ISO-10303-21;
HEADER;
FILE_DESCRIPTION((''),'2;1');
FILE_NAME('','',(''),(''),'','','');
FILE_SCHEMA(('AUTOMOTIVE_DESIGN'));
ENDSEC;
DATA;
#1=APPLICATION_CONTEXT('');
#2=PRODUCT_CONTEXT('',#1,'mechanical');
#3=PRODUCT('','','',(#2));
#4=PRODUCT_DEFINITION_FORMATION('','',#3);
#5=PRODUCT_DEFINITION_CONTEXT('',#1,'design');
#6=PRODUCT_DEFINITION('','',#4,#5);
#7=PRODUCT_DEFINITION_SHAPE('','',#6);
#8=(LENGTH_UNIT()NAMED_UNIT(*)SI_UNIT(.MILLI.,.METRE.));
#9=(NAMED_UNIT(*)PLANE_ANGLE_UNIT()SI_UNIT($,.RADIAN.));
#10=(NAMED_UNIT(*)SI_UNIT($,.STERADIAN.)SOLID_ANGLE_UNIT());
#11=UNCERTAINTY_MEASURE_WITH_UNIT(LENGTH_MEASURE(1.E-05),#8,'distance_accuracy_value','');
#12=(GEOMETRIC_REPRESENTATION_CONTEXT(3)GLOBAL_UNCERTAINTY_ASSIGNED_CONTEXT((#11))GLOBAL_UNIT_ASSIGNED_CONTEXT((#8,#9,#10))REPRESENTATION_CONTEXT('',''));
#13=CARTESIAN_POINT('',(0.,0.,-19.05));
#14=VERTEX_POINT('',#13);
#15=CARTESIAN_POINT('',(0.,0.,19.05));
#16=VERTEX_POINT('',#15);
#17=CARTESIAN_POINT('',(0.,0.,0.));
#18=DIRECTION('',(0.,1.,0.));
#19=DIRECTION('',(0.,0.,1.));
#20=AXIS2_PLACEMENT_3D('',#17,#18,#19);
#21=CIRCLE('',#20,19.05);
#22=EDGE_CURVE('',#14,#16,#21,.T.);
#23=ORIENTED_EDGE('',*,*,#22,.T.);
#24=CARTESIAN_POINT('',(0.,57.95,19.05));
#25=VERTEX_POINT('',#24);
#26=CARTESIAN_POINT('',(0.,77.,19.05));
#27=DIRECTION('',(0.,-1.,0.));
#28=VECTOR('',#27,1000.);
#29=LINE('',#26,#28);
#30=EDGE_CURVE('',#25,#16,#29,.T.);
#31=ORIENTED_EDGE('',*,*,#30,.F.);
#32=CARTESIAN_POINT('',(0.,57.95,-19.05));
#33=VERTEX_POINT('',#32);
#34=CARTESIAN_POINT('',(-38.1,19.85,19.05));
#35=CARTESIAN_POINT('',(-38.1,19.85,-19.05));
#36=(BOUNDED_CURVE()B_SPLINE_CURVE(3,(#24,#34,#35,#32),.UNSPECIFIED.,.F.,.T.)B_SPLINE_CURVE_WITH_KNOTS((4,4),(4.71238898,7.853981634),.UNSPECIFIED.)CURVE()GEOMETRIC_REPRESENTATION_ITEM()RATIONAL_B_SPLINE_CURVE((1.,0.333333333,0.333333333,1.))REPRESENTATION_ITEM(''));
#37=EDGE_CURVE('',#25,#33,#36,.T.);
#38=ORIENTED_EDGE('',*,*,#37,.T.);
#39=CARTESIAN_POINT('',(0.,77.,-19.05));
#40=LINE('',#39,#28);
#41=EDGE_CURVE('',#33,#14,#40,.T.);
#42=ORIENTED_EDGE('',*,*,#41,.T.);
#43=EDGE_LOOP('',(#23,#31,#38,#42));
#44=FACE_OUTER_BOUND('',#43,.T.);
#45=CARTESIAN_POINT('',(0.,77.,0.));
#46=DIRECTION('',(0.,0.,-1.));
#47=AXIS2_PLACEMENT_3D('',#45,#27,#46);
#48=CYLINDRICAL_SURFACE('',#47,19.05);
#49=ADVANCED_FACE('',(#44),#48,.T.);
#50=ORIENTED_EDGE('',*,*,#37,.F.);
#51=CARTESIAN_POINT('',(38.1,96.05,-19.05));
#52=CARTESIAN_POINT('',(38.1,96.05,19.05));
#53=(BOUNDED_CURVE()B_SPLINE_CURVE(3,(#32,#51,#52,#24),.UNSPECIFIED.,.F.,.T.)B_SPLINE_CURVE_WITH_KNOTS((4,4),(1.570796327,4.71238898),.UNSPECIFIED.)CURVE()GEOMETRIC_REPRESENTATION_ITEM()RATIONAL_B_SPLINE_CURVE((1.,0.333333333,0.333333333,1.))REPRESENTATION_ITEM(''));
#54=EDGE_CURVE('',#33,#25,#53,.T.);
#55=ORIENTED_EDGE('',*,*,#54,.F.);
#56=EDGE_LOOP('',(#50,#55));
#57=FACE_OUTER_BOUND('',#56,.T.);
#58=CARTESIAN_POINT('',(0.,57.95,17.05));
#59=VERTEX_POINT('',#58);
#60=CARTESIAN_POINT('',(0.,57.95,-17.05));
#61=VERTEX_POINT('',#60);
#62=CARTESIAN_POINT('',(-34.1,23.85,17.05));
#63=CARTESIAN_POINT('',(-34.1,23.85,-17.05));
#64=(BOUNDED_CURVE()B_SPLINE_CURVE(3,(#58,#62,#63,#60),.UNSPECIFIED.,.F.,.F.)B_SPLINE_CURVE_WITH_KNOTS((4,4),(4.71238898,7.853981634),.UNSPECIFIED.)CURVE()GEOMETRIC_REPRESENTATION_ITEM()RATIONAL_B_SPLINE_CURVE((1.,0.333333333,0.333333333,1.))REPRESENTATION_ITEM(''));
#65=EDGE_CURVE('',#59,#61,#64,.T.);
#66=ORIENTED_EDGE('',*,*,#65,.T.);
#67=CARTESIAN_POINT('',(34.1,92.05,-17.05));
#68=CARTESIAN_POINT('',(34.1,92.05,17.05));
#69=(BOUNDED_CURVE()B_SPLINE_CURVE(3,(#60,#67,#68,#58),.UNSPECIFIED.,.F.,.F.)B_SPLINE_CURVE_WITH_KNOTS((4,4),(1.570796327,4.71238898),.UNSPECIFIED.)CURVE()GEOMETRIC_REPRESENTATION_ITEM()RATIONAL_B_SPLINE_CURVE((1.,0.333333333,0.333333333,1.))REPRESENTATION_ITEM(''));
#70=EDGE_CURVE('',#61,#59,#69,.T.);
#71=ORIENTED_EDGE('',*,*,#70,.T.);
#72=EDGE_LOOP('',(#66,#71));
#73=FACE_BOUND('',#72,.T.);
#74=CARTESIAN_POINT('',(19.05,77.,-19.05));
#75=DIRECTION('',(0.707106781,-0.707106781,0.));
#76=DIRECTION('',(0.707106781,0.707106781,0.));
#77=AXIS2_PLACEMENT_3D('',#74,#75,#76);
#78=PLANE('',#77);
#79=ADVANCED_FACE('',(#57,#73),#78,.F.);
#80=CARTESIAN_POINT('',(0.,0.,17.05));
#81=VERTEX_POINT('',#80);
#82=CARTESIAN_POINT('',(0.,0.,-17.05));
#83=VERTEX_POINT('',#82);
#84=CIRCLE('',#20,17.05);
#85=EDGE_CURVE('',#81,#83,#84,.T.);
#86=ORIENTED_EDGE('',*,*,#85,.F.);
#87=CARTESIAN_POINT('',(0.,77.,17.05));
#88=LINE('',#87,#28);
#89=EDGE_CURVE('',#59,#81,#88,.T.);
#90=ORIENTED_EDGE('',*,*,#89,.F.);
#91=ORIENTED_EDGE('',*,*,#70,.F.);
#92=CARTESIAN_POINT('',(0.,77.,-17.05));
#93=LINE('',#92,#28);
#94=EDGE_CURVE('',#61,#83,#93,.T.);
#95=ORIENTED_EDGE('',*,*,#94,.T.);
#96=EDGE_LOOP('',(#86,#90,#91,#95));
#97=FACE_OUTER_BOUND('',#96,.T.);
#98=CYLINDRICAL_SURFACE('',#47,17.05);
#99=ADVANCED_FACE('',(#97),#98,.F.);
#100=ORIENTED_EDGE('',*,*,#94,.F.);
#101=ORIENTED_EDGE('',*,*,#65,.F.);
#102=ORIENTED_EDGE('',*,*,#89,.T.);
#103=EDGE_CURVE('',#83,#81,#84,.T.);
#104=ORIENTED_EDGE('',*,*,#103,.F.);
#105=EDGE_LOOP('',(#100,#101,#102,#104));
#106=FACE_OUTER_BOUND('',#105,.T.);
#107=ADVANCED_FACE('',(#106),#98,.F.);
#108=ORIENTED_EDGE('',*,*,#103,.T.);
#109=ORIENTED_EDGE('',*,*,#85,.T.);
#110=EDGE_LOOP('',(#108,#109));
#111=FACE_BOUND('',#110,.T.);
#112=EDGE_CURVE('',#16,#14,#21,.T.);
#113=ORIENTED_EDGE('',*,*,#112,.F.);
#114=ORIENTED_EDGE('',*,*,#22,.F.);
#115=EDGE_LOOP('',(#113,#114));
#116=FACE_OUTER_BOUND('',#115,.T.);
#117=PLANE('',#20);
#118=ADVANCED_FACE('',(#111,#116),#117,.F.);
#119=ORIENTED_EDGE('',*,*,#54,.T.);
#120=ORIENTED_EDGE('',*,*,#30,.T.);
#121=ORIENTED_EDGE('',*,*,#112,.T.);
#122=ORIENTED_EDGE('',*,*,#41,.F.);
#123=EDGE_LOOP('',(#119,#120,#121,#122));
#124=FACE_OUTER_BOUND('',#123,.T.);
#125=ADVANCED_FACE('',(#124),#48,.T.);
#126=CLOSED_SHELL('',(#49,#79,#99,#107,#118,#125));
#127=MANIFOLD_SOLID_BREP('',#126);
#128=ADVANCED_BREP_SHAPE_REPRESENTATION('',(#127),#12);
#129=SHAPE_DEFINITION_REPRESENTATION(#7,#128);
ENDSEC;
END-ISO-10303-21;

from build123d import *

# Parameters (mm, degrees)
SKETCH1_R               = 19.05
SKETCH1_R_2             = 17.05
BOSS_EXTRUDE1_DEPTH     = 77
CUT_EXTRUDE1_DEPTH      = 82.576988177
CUT_EXTRUDE1_DEPTH_BACK = 82.576988177


with BuildPart() as part:
    # Sketch1 → Boss-Extrude1 (new body)
    with BuildSketch(Plane(origin=(0, 0, 0), x_dir=(1, 0, 0), z_dir=(0, 1, 0))):
        with Locations(Location((0, 0, 0), (0, 0, 270))):
            Circle(SKETCH1_R)
        with Locations(Location((0, 0, 0), (0, 0, 270))):
            Circle(SKETCH1_R_2, mode=Mode.SUBTRACT)
    extrude(amount=BOSS_EXTRUDE1_DEPTH)

    # Sketch2 → Cut-Extrude1 (cut, two sides: drawn at the far end of the back side and taken through both)
    with BuildSketch(Plane.XY.offset(-CUT_EXTRUDE1_DEPTH_BACK)):
        Polygon((19.05, 77), (-19.05, 38.9), (-19.05, 77), align=None)
    extrude(amount=CUT_EXTRUDE1_DEPTH + CUT_EXTRUDE1_DEPTH_BACK, mode=Mode.SUBTRACT)


solid = part.part
